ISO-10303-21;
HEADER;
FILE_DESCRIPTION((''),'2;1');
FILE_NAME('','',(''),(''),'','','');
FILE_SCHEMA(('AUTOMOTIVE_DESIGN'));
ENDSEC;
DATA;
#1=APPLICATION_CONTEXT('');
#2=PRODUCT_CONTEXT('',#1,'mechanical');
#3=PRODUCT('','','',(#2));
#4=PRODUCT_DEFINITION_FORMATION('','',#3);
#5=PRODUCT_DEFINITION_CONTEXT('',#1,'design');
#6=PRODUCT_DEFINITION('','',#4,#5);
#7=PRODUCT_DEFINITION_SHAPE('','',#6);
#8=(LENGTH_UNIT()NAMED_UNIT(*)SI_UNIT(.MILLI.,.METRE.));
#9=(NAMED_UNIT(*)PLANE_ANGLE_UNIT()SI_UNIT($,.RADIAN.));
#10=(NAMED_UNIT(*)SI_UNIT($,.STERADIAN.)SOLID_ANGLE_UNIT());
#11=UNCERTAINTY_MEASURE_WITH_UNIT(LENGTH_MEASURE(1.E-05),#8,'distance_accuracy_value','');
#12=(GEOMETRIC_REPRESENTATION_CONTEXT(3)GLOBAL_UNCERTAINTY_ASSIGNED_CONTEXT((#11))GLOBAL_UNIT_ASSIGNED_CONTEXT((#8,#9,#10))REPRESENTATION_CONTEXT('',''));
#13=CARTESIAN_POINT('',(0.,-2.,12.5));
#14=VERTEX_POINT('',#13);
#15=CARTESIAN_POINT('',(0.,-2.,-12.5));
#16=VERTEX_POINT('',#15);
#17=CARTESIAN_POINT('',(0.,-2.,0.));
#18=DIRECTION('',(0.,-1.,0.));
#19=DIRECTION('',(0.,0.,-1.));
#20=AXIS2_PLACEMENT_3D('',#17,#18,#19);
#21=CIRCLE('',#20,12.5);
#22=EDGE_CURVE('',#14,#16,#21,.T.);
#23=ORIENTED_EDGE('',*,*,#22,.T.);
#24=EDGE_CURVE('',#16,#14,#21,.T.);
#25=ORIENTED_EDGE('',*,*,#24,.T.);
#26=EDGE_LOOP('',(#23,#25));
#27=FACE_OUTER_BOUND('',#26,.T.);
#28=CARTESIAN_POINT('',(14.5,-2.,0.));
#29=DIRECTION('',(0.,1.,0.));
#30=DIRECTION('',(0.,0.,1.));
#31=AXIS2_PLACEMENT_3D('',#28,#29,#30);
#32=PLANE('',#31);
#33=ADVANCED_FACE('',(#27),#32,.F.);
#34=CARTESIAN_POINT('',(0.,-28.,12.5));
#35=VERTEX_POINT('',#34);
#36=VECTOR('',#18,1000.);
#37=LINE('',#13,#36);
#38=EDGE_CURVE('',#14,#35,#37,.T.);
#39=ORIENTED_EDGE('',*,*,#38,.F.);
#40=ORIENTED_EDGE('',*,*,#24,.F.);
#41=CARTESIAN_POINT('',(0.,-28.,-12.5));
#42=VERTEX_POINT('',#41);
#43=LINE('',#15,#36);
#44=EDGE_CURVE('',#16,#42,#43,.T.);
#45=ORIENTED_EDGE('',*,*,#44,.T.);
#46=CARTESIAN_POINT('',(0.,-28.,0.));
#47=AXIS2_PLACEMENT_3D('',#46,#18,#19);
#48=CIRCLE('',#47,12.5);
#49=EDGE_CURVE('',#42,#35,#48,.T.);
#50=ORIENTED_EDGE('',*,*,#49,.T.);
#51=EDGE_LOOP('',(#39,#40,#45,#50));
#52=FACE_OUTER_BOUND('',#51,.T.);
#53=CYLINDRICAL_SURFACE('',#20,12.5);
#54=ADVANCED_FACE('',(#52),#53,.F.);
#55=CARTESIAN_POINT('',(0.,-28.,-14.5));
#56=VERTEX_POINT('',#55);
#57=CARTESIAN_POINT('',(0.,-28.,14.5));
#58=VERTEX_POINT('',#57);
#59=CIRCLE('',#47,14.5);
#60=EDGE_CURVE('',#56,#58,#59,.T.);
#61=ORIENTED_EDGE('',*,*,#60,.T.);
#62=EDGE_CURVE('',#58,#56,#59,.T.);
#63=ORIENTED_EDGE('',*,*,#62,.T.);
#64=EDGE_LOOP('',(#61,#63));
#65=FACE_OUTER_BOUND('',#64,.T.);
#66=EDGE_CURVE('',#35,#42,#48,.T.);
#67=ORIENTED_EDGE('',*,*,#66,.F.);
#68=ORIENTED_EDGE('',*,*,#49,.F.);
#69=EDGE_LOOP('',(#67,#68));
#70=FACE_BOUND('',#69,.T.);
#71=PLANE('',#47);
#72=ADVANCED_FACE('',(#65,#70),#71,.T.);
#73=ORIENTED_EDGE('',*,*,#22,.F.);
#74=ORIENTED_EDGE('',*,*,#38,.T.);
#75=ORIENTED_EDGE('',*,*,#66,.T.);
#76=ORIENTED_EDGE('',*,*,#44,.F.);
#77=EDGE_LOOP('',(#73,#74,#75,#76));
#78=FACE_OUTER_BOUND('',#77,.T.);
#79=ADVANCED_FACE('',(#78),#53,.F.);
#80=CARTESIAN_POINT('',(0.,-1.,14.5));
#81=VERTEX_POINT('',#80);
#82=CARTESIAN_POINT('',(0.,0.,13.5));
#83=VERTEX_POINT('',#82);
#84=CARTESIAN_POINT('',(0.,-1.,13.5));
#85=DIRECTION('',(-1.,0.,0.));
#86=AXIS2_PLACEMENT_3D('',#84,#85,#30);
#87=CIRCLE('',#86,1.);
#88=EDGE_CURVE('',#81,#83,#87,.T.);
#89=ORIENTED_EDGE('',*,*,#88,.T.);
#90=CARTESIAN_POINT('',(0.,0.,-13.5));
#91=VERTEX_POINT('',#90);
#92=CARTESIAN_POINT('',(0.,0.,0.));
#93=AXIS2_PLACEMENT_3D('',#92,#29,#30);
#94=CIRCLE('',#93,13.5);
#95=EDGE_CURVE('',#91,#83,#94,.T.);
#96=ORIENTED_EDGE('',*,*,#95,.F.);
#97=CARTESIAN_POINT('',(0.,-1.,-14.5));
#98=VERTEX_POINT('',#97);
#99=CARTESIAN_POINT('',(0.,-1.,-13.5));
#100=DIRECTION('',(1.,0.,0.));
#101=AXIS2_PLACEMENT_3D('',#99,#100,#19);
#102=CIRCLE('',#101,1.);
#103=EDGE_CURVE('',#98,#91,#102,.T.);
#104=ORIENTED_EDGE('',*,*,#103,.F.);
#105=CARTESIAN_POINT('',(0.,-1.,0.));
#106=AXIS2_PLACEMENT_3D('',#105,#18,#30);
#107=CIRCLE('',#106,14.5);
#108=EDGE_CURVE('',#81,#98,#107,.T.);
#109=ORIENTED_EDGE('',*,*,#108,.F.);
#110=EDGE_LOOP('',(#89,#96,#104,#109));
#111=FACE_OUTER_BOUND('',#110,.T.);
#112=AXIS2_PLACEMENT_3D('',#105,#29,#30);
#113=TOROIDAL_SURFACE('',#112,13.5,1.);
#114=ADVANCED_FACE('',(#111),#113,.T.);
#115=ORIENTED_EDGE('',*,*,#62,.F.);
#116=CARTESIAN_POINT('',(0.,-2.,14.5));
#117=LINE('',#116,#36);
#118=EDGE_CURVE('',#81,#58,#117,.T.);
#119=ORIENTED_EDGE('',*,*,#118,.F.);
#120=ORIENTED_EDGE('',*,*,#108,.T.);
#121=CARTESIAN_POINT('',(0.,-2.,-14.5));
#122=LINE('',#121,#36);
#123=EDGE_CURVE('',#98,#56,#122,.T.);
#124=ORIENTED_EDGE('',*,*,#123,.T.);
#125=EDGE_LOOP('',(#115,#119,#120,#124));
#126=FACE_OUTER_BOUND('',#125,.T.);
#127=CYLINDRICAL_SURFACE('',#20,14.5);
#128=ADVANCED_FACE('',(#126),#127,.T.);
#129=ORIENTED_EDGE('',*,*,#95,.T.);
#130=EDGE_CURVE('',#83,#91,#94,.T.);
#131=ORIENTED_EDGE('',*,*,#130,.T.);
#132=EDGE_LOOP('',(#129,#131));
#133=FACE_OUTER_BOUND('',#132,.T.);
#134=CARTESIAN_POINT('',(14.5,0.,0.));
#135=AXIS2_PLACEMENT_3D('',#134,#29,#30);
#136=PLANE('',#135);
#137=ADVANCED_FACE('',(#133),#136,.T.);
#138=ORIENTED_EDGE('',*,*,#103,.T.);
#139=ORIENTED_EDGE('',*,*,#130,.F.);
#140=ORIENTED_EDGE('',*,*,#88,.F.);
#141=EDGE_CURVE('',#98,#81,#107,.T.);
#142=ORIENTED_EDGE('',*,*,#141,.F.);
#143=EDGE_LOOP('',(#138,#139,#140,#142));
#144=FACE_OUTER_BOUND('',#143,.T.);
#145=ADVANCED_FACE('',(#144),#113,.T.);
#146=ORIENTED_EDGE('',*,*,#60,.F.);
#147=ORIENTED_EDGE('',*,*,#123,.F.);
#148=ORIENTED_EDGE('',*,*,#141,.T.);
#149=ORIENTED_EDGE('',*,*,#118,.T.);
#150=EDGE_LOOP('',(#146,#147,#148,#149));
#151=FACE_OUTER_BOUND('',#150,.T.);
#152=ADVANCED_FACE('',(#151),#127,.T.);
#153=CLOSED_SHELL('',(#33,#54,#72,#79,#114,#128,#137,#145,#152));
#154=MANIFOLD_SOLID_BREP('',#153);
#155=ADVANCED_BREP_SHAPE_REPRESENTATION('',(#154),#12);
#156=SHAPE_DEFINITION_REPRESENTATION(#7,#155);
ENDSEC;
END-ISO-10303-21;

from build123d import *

# Parameters (mm, degrees)
SKETCH_1_W   = 2
SKETCH_1_H   = 26
SKETCH_1_H_2 = 2
SKETCH_1_W_2 = 12.5
FILLET_1_R   = 1


with BuildPart() as part:
    # 草图1 → 旋转1 (revolve)
    with BuildSketch(Plane.XY, mode=Mode.PRIVATE) as revolve_1_sk:
        with Locations((13.5, -15)):
            Rectangle(SKETCH_1_W, SKETCH_1_H)
        with Locations((13.5, -1)):
            Rectangle(SKETCH_1_W, SKETCH_1_H_2)
        with Locations((6.25, -1)):
            Rectangle(SKETCH_1_W_2, SKETCH_1_H_2)
    revolve(revolve_1_sk.sketch.rotate(Axis((0, -2, 0), (0, 1, 0)), 90), axis=Axis((0, -2, 0), (0, 1, 0)))

    # 圆角1
    fillet_1_edges = [part.edges().sort_by_distance(p)[0] for p in [
        (0, 0, 14.5),
    ]]
    fillet(fillet_1_edges, radius=FILLET_1_R)


solid = part.part
